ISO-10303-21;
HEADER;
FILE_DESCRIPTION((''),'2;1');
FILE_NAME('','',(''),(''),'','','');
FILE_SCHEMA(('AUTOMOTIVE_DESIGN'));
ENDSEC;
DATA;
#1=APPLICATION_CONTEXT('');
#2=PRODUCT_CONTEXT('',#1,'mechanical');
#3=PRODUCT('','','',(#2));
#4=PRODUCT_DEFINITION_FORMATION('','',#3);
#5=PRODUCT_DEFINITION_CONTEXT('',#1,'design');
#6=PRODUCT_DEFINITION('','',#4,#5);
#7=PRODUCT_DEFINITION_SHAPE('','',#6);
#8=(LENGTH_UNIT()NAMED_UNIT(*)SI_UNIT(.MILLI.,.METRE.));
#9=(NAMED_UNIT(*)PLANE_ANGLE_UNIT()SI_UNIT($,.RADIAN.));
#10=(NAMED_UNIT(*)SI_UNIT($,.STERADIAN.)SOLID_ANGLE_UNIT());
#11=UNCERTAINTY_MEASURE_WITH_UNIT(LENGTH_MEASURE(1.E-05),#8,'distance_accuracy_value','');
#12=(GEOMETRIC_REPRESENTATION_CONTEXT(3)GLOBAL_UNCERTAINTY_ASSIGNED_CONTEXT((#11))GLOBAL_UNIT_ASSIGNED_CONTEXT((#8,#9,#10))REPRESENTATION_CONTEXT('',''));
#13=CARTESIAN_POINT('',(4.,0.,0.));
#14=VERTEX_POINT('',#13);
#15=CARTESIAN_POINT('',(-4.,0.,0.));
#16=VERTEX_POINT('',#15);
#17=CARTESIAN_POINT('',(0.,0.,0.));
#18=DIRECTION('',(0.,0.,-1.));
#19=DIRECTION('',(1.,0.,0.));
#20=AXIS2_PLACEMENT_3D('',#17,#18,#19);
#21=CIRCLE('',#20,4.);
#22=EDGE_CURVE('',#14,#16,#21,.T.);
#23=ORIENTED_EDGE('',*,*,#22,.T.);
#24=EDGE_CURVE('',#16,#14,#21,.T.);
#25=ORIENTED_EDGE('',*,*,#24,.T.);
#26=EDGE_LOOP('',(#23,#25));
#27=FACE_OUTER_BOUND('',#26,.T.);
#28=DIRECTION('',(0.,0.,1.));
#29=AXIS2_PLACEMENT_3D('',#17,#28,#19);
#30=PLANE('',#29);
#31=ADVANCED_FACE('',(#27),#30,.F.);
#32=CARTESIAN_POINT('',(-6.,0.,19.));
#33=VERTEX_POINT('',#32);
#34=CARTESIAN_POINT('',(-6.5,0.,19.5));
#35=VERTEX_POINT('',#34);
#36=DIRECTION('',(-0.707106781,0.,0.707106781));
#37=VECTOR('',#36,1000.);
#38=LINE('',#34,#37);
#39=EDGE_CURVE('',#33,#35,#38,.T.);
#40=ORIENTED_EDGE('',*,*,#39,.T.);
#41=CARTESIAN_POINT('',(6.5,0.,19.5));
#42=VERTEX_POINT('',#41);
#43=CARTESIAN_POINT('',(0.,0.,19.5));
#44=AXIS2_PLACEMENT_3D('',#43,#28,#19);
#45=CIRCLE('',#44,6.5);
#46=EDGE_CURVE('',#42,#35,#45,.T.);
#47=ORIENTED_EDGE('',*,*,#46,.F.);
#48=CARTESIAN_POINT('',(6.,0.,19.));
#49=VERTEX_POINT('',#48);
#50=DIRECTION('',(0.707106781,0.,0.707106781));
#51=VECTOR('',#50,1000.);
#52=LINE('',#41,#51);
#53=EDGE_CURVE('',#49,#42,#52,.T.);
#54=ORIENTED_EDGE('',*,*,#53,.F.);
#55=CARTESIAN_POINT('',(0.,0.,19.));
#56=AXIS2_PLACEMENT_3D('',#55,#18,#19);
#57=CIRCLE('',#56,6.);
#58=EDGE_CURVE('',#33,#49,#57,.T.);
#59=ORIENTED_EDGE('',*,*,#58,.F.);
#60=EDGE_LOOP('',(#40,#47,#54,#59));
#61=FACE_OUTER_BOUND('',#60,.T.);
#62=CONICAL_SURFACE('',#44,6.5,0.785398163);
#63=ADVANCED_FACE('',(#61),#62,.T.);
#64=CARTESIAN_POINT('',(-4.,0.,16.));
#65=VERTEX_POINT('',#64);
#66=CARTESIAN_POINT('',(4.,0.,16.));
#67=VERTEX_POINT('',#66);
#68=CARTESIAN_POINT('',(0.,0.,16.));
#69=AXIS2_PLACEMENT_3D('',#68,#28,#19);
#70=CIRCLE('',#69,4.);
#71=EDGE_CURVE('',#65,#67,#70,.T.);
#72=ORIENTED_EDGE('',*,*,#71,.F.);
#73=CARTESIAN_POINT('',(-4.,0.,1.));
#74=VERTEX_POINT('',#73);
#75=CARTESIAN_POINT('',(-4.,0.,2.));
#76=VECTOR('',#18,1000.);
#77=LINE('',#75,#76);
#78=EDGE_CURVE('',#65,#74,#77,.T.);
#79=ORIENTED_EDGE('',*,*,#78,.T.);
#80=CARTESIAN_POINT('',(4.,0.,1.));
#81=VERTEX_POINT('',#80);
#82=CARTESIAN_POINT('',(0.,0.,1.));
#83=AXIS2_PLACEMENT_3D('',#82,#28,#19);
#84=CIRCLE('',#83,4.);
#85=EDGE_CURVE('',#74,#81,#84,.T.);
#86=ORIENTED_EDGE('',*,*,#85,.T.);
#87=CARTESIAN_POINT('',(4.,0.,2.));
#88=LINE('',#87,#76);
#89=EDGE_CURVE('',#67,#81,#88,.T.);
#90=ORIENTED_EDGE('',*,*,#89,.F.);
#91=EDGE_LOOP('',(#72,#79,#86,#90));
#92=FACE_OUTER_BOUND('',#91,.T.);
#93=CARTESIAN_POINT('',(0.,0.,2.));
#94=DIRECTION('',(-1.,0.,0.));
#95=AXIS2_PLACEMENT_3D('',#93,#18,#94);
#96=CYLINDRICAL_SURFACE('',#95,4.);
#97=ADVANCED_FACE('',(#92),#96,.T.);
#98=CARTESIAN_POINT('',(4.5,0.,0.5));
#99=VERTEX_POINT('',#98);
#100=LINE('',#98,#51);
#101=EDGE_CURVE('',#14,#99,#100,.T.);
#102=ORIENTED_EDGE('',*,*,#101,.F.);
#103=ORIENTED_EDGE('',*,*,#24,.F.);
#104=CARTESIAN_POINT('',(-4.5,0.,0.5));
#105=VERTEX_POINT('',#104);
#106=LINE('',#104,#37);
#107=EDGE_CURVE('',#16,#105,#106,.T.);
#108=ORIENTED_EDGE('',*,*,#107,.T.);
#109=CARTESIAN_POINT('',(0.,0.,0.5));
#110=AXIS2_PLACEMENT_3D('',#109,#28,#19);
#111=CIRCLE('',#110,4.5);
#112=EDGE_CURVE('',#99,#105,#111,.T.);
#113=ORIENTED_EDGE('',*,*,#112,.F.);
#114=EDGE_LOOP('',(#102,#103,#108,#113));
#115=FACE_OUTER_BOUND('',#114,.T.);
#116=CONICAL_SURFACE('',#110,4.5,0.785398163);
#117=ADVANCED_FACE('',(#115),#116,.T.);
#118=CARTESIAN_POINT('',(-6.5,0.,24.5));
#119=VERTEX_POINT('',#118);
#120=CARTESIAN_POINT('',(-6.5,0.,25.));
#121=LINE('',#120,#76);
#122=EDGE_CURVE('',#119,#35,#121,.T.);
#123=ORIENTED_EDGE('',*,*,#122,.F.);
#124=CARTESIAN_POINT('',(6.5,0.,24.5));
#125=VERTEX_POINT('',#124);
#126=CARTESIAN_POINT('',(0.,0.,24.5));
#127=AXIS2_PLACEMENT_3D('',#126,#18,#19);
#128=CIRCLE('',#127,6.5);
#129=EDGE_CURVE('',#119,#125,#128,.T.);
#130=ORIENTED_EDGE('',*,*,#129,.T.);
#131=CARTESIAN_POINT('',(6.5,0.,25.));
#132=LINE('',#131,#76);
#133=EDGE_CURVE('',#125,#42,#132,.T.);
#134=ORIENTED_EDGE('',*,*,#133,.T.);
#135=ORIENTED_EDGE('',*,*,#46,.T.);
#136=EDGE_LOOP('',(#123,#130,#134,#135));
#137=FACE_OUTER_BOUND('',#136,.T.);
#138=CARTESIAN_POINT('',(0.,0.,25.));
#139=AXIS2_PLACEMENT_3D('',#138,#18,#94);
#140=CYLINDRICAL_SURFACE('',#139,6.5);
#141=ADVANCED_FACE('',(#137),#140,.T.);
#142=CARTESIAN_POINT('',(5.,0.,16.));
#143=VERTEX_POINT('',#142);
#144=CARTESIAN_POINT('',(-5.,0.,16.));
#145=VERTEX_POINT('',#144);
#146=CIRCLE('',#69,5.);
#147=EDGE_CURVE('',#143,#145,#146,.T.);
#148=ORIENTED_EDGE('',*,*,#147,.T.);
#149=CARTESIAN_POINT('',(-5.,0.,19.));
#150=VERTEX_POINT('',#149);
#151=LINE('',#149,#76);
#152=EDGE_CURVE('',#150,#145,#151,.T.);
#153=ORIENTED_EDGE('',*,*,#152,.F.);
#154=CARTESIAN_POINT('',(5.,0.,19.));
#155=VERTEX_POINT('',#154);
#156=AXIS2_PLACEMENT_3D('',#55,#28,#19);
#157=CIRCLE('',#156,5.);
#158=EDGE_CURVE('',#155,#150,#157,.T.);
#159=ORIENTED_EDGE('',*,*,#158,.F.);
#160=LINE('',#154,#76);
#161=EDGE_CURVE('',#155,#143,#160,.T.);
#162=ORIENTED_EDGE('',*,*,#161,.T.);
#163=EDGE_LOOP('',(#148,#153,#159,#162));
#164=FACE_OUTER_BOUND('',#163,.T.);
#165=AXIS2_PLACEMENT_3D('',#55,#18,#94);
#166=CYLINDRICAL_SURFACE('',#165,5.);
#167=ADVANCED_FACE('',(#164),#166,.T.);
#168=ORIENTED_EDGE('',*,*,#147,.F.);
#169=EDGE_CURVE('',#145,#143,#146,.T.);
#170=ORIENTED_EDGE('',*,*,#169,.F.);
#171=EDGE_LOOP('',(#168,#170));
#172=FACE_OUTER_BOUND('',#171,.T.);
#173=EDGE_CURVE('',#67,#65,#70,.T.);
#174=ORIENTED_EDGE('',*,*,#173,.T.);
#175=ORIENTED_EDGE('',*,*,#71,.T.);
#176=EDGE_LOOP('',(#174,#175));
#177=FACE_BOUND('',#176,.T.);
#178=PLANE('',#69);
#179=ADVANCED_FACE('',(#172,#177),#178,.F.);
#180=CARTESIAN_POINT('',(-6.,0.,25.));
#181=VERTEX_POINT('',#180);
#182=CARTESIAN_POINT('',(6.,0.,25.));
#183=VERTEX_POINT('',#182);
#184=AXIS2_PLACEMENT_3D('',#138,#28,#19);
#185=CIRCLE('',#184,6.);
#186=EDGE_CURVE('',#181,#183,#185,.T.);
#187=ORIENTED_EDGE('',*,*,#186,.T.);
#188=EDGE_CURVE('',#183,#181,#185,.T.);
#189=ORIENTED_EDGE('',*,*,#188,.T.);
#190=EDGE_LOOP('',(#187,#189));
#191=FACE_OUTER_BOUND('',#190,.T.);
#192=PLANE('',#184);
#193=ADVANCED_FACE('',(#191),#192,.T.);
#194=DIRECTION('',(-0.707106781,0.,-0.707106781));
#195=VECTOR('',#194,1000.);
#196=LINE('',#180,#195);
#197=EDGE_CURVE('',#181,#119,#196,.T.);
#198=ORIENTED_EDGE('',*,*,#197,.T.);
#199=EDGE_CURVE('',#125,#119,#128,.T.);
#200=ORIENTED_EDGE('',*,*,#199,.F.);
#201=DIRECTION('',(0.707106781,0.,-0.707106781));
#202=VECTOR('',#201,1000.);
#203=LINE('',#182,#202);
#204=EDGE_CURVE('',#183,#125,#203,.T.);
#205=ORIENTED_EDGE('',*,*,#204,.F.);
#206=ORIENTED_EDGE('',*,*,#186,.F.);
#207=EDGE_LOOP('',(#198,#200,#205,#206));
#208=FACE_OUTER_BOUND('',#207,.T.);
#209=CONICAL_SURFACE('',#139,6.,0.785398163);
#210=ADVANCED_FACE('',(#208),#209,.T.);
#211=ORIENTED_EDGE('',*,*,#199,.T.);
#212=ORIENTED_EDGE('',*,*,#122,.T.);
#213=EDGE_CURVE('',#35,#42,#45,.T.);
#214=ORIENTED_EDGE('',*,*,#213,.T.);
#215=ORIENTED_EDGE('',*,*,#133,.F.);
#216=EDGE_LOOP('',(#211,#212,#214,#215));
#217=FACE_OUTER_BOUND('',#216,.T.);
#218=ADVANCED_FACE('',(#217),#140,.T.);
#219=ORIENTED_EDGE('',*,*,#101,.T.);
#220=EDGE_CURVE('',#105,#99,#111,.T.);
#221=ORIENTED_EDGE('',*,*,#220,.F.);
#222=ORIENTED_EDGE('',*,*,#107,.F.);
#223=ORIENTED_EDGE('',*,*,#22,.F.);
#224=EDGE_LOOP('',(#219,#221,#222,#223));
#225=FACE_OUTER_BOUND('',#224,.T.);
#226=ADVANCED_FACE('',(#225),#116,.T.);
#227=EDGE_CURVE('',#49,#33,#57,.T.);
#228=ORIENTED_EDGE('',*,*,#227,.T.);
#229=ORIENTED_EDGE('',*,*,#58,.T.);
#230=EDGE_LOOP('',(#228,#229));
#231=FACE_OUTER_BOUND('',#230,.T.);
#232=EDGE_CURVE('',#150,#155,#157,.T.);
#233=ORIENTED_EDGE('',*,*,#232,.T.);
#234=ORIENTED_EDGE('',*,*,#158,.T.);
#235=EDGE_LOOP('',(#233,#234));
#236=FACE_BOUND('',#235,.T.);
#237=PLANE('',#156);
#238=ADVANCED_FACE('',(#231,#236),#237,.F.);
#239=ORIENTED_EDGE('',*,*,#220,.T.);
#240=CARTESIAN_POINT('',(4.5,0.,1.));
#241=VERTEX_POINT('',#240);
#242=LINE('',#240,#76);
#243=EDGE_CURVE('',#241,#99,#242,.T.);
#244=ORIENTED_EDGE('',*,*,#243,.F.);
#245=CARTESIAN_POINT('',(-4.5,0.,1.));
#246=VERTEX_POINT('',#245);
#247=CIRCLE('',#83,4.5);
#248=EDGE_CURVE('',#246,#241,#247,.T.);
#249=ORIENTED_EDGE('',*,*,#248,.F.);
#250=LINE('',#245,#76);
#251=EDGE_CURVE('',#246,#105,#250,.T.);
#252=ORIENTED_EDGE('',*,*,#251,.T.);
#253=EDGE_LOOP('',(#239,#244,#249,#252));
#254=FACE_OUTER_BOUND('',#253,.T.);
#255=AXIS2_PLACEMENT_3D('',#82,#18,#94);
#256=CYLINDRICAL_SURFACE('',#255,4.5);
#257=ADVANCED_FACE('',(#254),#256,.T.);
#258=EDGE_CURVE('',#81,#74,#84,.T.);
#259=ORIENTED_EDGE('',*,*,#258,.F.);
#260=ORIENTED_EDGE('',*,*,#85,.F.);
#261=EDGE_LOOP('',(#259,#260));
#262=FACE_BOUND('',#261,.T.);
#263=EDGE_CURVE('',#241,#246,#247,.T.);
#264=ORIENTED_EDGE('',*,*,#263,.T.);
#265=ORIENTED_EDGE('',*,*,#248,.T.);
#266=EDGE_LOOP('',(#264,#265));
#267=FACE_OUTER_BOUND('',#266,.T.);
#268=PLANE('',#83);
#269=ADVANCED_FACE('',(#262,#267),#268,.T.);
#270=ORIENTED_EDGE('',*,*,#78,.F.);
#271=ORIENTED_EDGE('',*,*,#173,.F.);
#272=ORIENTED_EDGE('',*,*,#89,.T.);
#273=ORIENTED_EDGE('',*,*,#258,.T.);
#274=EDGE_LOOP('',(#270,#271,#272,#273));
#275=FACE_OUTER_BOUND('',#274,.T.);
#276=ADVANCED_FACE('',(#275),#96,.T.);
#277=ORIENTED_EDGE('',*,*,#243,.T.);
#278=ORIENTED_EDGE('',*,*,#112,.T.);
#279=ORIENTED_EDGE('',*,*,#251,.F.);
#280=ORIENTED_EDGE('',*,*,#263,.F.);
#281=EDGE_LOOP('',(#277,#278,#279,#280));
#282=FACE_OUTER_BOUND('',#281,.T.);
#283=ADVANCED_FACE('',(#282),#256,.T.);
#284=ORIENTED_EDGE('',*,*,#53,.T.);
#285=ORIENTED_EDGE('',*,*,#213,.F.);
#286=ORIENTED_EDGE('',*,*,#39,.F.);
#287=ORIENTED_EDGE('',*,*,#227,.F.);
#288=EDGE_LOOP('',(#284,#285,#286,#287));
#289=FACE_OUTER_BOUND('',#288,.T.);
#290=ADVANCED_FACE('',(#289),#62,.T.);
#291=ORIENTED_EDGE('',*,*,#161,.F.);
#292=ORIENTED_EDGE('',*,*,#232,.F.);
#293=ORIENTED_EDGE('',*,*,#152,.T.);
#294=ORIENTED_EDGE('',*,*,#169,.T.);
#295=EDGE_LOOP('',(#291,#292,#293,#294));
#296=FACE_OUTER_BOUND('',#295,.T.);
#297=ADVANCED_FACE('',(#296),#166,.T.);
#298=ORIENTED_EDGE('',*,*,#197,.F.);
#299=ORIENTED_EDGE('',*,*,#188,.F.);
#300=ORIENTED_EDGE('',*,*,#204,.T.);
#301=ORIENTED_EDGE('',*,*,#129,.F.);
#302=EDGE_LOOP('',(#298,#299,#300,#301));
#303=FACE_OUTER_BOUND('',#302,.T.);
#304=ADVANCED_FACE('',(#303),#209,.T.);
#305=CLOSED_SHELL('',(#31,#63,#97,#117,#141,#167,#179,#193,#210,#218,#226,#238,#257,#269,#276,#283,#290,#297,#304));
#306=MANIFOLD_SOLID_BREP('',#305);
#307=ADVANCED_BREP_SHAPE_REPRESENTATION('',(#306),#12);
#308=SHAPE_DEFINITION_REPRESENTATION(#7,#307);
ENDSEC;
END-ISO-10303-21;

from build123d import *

# Parameters (mm, degrees)
SKETCH1_R           = 4.5
BOSS_EXTRUDE1_DEPTH = 1
SKETCH2_R           = 4
BOSS_EXTRUDE2_DEPTH = 1
SKETCH3_R           = 4
BOSS_EXTRUDE3_DEPTH = 14
SKETCH4_R           = 5
BOSS_EXTRUDE4_DEPTH = 3
SKETCH5_R           = 6.5
BOSS_EXTRUDE5_DEPTH = 6
CHAMFER1_SIZE       = 0.5


with BuildPart() as part:
    # Sketch1 → Boss-Extrude1 (new body)
    with BuildSketch(Plane.XY):
        Circle(SKETCH1_R)
    extrude(amount=BOSS_EXTRUDE1_DEPTH)

    # Sketch2 → Boss-Extrude2 (add)
    with BuildSketch(Plane.XY.offset(1)):
        Circle(SKETCH2_R)
    extrude(amount=BOSS_EXTRUDE2_DEPTH)

    # Sketch3 → Boss-Extrude3 (add)
    with BuildSketch(Plane.XY.offset(2)):
        Circle(SKETCH3_R)
    extrude(amount=BOSS_EXTRUDE3_DEPTH)

    # Sketch4 → Boss-Extrude4 (add)
    with BuildSketch(Plane.XY.offset(16)):
        Circle(SKETCH4_R)
    extrude(amount=BOSS_EXTRUDE4_DEPTH)

    # Sketch5 → Boss-Extrude5 (add)
    with BuildSketch(Plane.XY.offset(19)):
        Circle(SKETCH5_R)
    extrude(amount=BOSS_EXTRUDE5_DEPTH)

    # Chamfer1
    chamfer1_edges = [part.edges().sort_by_distance(p)[0] for p in [
        (-6.5, 0, 19),
        (-6.5, 0, 25),
        (-4.5, 0, 0),
    ]]
    chamfer(chamfer1_edges, length=CHAMFER1_SIZE)


solid = part.part
